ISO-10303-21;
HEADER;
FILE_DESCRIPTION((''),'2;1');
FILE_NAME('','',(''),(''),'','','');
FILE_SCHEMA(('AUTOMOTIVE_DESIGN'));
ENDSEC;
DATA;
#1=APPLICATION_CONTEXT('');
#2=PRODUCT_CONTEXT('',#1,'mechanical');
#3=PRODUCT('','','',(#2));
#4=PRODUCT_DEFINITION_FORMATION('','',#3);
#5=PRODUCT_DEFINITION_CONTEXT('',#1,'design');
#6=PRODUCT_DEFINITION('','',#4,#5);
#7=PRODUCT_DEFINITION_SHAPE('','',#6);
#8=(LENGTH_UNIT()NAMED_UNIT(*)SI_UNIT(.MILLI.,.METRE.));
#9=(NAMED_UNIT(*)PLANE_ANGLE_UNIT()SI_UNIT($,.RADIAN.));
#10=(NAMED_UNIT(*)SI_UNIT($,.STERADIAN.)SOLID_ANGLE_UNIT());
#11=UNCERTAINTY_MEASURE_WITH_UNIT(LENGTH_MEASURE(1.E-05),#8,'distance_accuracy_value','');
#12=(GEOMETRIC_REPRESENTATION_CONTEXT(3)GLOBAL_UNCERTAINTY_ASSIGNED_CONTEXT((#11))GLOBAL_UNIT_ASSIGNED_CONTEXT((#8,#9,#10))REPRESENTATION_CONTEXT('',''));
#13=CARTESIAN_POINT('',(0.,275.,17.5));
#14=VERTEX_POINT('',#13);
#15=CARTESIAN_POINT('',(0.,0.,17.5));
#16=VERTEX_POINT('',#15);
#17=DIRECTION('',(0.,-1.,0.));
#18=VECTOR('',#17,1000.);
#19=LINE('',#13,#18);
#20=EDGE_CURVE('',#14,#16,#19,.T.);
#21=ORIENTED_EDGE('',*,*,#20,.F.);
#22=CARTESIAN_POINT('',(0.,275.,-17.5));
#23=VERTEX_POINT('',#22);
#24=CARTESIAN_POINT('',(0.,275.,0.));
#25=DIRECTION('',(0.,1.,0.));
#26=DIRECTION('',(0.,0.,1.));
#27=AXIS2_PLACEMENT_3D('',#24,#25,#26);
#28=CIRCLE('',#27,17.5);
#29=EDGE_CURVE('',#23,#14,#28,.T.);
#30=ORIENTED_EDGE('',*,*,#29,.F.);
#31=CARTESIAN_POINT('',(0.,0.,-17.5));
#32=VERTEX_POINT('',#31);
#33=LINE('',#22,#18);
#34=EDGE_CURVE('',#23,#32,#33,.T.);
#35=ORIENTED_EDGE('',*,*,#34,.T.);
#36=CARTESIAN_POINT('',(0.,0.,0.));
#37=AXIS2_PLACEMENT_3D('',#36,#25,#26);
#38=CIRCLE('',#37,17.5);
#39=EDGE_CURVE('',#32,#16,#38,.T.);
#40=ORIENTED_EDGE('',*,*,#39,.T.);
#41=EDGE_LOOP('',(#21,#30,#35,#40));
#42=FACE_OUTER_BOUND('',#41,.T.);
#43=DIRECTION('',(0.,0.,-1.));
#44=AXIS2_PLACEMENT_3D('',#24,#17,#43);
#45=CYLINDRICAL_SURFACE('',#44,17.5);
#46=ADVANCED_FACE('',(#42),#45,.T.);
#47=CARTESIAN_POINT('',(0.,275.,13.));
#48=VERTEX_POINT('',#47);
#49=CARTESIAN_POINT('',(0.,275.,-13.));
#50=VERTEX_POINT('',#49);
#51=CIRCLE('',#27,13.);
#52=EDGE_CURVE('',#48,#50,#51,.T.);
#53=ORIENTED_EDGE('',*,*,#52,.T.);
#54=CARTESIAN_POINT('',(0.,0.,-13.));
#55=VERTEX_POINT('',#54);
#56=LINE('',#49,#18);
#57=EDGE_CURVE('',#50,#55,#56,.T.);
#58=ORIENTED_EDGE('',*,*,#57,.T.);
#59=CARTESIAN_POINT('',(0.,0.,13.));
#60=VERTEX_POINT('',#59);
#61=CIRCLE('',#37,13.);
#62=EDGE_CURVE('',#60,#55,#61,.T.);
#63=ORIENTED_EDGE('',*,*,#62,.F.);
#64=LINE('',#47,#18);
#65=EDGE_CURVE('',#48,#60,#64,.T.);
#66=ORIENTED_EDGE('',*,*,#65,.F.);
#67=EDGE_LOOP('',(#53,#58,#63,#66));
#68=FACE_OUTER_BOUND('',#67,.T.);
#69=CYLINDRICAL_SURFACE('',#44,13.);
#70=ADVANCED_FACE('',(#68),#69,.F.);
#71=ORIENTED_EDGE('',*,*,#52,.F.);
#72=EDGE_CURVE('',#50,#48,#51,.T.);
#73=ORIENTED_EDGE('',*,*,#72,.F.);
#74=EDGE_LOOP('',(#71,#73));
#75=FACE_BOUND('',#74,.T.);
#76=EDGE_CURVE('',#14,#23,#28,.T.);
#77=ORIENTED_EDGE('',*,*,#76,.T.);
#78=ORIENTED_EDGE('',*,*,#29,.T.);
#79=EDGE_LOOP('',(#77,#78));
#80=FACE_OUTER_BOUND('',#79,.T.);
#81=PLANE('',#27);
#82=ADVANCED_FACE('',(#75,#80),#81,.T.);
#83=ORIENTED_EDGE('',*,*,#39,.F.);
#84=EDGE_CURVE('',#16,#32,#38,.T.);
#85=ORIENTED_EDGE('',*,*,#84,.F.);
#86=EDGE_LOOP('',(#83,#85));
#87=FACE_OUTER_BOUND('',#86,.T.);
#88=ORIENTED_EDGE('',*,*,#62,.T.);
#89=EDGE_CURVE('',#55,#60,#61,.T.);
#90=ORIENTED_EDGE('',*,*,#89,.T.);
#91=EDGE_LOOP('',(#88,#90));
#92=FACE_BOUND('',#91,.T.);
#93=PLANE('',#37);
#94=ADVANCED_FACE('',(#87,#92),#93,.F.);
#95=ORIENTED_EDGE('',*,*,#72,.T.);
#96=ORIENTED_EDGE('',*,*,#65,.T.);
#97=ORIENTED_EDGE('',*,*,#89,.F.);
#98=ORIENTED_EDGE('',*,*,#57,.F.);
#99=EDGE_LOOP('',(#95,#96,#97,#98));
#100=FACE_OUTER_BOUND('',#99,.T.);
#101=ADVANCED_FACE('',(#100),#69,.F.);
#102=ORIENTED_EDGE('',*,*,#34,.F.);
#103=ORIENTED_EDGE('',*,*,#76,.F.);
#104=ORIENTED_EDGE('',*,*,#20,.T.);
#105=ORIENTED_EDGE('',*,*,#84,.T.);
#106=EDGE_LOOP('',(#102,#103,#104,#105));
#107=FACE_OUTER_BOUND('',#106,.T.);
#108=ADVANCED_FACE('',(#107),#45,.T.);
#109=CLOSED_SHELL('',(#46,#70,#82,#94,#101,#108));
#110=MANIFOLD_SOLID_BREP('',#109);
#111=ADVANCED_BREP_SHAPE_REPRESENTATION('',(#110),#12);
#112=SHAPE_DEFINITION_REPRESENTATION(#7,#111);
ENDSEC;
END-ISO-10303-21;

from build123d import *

# Parameters (mm, degrees)
SKETCH_1_R      = 17.5
EXTRUDE_1_DEPTH = 275
SHELL_1_T       = -4.5


with BuildPart() as part:
    # 草图1 → 凸台-拉伸1 (new body)
    with BuildSketch(Plane(origin=(0, 0, 0), x_dir=(1, 0, 0), z_dir=(0, 1, 0))):
        with Locations(Location((0, 0, 0), (0, 0, 270))):
            Circle(SKETCH_1_R)
    extrude(amount=EXTRUDE_1_DEPTH)

    # 抽壳1
    shell_1_openings = [part.faces().sort_by_distance(p)[0] for p in [
        (0, 275, 0),
        (0, 0, 0),
    ]]
    offset(amount=SHELL_1_T, openings=shell_1_openings, kind=Kind.INTERSECTION)


solid = part.part
